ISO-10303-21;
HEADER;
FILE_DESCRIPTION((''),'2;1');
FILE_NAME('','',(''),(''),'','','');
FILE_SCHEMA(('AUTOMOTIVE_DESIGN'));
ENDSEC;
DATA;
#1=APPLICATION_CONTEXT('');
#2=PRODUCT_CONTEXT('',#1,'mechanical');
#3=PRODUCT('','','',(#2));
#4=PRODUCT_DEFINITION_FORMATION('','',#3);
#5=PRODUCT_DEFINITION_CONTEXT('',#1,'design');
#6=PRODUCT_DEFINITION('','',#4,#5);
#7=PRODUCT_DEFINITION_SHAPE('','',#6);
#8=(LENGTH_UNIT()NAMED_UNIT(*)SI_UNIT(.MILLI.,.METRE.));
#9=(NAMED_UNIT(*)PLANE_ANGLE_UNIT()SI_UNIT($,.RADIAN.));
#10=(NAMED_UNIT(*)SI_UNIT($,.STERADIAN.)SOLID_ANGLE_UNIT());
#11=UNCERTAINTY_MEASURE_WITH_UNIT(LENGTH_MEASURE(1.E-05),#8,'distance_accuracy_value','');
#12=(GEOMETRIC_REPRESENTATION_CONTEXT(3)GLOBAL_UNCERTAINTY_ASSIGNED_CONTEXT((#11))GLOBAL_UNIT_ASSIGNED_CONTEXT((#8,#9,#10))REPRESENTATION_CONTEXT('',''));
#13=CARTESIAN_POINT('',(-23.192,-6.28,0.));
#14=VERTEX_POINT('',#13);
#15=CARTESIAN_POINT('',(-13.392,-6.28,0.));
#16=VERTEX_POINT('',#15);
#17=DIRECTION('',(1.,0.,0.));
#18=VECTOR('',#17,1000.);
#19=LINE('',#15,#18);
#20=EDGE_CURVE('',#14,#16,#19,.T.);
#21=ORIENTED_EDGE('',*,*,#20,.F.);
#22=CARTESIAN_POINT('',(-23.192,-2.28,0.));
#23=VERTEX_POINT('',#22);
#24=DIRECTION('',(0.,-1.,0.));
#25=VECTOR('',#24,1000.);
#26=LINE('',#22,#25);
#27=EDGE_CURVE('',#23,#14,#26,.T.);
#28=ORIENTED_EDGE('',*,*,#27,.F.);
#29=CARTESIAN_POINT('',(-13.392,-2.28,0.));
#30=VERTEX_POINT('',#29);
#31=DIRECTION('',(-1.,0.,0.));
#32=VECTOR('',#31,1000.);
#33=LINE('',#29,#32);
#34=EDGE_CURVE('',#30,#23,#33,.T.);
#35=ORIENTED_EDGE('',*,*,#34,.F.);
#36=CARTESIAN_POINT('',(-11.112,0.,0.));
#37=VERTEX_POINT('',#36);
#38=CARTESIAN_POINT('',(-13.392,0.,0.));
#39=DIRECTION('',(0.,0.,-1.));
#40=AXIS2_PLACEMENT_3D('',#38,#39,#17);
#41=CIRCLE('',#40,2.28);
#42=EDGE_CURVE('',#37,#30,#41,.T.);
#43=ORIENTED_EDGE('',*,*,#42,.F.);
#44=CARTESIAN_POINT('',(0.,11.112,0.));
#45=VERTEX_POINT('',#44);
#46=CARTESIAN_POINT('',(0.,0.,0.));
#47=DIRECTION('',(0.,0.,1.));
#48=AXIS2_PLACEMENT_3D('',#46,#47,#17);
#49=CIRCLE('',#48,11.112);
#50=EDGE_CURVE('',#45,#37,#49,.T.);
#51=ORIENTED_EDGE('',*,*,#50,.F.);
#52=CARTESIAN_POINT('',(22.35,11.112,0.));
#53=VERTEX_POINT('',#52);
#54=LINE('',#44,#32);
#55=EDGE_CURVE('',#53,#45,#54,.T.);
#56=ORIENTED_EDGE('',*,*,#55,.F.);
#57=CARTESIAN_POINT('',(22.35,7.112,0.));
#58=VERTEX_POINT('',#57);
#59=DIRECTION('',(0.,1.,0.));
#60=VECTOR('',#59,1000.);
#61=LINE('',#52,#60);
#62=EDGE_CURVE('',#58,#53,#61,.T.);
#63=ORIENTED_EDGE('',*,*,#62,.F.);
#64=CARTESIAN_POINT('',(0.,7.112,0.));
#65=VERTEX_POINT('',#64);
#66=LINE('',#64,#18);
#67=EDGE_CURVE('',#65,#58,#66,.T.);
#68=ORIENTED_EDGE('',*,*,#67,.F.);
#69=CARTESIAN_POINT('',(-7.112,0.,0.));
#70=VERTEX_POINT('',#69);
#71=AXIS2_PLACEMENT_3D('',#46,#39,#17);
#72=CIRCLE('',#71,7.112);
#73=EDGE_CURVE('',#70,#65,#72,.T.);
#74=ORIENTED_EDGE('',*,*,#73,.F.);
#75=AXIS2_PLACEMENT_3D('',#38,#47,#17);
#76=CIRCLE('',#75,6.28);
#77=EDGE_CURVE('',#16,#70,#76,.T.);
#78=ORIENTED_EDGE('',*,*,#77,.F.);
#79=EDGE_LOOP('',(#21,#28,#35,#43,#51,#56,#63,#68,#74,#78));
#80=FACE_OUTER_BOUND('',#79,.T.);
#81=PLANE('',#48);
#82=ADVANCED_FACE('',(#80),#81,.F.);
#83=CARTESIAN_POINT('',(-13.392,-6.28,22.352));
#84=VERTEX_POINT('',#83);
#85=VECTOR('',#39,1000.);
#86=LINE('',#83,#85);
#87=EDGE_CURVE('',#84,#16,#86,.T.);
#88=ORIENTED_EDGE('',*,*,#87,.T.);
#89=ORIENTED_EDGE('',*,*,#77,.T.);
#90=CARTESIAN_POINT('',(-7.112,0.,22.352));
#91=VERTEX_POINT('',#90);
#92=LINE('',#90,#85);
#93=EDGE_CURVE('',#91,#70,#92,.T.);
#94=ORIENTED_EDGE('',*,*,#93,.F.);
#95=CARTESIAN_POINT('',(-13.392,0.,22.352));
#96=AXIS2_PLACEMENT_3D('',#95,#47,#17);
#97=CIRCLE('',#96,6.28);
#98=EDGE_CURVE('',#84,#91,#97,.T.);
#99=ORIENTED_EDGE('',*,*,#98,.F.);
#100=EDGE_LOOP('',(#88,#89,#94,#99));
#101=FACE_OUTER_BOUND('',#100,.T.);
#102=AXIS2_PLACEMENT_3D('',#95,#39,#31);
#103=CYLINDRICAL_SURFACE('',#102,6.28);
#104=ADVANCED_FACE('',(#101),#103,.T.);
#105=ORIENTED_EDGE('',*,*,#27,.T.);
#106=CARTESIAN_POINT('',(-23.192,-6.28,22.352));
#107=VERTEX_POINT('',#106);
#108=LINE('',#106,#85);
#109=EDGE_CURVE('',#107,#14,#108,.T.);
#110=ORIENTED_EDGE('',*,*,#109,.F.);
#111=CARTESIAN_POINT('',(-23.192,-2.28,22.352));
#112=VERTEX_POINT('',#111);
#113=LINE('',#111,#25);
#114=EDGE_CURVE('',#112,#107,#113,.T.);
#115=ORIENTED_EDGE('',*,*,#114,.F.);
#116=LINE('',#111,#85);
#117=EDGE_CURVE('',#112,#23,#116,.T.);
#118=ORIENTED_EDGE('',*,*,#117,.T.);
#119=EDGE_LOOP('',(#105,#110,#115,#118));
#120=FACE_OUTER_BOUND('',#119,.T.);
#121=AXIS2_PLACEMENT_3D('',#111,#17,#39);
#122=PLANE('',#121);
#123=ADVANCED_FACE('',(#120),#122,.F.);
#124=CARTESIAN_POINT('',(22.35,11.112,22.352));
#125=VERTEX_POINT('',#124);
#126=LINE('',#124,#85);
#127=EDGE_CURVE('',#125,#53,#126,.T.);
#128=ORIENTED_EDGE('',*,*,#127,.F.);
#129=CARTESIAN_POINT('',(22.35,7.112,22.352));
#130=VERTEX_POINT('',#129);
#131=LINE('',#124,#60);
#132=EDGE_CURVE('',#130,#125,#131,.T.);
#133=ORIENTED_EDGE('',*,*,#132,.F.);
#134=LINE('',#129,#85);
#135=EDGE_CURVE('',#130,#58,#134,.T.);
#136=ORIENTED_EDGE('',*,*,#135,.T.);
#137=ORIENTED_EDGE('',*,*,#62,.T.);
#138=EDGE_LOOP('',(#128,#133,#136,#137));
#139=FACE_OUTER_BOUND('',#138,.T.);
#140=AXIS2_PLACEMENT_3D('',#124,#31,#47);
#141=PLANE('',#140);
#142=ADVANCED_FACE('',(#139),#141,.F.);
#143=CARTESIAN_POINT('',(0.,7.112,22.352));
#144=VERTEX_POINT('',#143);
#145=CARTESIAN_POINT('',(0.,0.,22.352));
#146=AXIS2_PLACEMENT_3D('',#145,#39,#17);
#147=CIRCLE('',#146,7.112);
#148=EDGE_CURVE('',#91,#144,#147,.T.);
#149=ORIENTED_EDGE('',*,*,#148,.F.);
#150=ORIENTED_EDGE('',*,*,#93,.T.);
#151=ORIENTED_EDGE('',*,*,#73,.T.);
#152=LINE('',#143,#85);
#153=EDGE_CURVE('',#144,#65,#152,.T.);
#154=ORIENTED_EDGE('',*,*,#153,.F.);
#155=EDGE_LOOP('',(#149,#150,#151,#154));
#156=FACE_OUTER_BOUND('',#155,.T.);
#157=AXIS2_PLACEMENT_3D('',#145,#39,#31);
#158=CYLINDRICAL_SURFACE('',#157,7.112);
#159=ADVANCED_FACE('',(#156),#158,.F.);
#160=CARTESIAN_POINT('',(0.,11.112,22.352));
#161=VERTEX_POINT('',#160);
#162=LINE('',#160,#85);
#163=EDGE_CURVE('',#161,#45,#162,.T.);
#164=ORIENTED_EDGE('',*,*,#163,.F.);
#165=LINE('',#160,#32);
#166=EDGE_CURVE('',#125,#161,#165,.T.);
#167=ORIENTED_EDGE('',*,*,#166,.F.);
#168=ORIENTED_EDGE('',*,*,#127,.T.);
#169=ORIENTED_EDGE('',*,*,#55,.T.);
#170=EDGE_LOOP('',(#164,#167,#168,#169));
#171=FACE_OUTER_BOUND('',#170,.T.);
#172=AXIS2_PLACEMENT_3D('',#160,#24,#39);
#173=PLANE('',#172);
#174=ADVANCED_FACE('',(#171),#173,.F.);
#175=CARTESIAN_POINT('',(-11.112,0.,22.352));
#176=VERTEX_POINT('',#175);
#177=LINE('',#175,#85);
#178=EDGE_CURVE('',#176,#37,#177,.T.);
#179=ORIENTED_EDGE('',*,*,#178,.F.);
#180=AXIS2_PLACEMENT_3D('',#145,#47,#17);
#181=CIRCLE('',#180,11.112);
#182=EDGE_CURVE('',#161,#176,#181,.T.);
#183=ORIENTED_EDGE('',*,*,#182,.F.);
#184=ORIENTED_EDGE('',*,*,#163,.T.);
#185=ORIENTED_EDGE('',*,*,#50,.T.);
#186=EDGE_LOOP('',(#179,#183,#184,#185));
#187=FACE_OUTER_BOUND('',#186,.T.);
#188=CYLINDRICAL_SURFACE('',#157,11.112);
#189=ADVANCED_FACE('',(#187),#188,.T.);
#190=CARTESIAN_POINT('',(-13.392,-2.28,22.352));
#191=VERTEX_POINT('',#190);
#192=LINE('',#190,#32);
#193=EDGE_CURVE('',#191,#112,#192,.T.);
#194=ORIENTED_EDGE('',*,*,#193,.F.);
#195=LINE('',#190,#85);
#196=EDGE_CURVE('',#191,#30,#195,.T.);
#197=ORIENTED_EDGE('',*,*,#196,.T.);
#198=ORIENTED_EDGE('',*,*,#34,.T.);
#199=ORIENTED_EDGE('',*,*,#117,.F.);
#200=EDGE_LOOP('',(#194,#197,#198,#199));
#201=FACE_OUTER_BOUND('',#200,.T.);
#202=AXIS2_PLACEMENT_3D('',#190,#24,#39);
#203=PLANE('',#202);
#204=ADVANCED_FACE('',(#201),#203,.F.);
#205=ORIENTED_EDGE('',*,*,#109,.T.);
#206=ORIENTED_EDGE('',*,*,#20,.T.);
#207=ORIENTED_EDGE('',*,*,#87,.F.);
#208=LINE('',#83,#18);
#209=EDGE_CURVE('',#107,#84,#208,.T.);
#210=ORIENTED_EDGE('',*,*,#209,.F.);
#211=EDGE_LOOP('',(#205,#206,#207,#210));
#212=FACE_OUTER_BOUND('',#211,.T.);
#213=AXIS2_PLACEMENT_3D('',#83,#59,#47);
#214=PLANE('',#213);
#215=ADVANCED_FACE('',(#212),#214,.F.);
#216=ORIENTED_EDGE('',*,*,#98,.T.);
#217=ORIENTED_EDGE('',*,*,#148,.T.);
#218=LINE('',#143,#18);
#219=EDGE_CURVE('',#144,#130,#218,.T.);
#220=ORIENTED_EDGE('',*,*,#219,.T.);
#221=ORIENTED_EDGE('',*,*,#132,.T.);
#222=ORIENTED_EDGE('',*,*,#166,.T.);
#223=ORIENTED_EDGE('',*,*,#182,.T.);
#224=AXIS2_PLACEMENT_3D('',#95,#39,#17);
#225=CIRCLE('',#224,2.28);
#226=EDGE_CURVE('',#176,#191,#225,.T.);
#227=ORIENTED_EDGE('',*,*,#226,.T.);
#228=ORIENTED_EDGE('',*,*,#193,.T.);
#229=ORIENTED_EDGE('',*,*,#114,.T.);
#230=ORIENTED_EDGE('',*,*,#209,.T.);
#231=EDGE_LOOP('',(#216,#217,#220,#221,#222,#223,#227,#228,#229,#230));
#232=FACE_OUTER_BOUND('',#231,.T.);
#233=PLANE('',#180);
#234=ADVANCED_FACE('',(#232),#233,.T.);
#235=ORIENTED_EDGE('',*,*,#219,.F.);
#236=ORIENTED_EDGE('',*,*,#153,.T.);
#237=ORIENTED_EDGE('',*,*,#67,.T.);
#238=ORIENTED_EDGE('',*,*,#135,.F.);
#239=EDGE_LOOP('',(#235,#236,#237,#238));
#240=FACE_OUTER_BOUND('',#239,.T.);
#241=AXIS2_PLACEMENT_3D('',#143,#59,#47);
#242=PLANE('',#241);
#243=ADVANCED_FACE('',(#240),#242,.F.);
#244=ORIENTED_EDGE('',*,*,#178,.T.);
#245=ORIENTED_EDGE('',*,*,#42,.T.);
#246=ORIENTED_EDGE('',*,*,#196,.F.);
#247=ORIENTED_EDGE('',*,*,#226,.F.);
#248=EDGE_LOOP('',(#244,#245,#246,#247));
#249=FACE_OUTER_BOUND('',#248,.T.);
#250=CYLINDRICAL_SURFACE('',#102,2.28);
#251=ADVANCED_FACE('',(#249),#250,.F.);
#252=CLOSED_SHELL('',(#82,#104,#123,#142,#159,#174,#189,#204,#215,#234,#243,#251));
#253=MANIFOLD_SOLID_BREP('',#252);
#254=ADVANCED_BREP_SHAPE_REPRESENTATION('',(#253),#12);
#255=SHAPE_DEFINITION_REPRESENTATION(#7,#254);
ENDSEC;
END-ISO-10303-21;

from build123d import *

# Parameters (mm, degrees)
BOSS_EXTRUDE1_DEPTH = 22.352


with BuildPart() as part:
    # Sketch1 → Boss-Extrude1 (new body)
    with BuildSketch(Plane.XY):
        with BuildLine():
            Line((0, 11.112), (22.35, 11.112))
            Line((22.35, 11.112), (22.35, 7.112))
            Line((22.35, 7.112), (0, 7.112))
            ThreePointArc((0, 7.112), (-5.028943428, 5.028943428), (-7.112, 0))
            ThreePointArc((-7.112, 0), (-8.951369414, -4.440630586), (-13.392, -6.28))
            Line((-13.392, -6.28), (-23.192, -6.28))
            Line((-23.192, -6.28), (-23.192, -2.28))
            Line((-23.192, -2.28), (-13.392, -2.28))
            ThreePointArc((-13.392, -2.28), (-11.779796539, -1.612203461), (-11.112, 0))
            ThreePointArc((-11.112, 0), (-7.857370553, 7.857370553), (0, 11.112))
        make_face()
    extrude(amount=BOSS_EXTRUDE1_DEPTH)


solid = part.part
